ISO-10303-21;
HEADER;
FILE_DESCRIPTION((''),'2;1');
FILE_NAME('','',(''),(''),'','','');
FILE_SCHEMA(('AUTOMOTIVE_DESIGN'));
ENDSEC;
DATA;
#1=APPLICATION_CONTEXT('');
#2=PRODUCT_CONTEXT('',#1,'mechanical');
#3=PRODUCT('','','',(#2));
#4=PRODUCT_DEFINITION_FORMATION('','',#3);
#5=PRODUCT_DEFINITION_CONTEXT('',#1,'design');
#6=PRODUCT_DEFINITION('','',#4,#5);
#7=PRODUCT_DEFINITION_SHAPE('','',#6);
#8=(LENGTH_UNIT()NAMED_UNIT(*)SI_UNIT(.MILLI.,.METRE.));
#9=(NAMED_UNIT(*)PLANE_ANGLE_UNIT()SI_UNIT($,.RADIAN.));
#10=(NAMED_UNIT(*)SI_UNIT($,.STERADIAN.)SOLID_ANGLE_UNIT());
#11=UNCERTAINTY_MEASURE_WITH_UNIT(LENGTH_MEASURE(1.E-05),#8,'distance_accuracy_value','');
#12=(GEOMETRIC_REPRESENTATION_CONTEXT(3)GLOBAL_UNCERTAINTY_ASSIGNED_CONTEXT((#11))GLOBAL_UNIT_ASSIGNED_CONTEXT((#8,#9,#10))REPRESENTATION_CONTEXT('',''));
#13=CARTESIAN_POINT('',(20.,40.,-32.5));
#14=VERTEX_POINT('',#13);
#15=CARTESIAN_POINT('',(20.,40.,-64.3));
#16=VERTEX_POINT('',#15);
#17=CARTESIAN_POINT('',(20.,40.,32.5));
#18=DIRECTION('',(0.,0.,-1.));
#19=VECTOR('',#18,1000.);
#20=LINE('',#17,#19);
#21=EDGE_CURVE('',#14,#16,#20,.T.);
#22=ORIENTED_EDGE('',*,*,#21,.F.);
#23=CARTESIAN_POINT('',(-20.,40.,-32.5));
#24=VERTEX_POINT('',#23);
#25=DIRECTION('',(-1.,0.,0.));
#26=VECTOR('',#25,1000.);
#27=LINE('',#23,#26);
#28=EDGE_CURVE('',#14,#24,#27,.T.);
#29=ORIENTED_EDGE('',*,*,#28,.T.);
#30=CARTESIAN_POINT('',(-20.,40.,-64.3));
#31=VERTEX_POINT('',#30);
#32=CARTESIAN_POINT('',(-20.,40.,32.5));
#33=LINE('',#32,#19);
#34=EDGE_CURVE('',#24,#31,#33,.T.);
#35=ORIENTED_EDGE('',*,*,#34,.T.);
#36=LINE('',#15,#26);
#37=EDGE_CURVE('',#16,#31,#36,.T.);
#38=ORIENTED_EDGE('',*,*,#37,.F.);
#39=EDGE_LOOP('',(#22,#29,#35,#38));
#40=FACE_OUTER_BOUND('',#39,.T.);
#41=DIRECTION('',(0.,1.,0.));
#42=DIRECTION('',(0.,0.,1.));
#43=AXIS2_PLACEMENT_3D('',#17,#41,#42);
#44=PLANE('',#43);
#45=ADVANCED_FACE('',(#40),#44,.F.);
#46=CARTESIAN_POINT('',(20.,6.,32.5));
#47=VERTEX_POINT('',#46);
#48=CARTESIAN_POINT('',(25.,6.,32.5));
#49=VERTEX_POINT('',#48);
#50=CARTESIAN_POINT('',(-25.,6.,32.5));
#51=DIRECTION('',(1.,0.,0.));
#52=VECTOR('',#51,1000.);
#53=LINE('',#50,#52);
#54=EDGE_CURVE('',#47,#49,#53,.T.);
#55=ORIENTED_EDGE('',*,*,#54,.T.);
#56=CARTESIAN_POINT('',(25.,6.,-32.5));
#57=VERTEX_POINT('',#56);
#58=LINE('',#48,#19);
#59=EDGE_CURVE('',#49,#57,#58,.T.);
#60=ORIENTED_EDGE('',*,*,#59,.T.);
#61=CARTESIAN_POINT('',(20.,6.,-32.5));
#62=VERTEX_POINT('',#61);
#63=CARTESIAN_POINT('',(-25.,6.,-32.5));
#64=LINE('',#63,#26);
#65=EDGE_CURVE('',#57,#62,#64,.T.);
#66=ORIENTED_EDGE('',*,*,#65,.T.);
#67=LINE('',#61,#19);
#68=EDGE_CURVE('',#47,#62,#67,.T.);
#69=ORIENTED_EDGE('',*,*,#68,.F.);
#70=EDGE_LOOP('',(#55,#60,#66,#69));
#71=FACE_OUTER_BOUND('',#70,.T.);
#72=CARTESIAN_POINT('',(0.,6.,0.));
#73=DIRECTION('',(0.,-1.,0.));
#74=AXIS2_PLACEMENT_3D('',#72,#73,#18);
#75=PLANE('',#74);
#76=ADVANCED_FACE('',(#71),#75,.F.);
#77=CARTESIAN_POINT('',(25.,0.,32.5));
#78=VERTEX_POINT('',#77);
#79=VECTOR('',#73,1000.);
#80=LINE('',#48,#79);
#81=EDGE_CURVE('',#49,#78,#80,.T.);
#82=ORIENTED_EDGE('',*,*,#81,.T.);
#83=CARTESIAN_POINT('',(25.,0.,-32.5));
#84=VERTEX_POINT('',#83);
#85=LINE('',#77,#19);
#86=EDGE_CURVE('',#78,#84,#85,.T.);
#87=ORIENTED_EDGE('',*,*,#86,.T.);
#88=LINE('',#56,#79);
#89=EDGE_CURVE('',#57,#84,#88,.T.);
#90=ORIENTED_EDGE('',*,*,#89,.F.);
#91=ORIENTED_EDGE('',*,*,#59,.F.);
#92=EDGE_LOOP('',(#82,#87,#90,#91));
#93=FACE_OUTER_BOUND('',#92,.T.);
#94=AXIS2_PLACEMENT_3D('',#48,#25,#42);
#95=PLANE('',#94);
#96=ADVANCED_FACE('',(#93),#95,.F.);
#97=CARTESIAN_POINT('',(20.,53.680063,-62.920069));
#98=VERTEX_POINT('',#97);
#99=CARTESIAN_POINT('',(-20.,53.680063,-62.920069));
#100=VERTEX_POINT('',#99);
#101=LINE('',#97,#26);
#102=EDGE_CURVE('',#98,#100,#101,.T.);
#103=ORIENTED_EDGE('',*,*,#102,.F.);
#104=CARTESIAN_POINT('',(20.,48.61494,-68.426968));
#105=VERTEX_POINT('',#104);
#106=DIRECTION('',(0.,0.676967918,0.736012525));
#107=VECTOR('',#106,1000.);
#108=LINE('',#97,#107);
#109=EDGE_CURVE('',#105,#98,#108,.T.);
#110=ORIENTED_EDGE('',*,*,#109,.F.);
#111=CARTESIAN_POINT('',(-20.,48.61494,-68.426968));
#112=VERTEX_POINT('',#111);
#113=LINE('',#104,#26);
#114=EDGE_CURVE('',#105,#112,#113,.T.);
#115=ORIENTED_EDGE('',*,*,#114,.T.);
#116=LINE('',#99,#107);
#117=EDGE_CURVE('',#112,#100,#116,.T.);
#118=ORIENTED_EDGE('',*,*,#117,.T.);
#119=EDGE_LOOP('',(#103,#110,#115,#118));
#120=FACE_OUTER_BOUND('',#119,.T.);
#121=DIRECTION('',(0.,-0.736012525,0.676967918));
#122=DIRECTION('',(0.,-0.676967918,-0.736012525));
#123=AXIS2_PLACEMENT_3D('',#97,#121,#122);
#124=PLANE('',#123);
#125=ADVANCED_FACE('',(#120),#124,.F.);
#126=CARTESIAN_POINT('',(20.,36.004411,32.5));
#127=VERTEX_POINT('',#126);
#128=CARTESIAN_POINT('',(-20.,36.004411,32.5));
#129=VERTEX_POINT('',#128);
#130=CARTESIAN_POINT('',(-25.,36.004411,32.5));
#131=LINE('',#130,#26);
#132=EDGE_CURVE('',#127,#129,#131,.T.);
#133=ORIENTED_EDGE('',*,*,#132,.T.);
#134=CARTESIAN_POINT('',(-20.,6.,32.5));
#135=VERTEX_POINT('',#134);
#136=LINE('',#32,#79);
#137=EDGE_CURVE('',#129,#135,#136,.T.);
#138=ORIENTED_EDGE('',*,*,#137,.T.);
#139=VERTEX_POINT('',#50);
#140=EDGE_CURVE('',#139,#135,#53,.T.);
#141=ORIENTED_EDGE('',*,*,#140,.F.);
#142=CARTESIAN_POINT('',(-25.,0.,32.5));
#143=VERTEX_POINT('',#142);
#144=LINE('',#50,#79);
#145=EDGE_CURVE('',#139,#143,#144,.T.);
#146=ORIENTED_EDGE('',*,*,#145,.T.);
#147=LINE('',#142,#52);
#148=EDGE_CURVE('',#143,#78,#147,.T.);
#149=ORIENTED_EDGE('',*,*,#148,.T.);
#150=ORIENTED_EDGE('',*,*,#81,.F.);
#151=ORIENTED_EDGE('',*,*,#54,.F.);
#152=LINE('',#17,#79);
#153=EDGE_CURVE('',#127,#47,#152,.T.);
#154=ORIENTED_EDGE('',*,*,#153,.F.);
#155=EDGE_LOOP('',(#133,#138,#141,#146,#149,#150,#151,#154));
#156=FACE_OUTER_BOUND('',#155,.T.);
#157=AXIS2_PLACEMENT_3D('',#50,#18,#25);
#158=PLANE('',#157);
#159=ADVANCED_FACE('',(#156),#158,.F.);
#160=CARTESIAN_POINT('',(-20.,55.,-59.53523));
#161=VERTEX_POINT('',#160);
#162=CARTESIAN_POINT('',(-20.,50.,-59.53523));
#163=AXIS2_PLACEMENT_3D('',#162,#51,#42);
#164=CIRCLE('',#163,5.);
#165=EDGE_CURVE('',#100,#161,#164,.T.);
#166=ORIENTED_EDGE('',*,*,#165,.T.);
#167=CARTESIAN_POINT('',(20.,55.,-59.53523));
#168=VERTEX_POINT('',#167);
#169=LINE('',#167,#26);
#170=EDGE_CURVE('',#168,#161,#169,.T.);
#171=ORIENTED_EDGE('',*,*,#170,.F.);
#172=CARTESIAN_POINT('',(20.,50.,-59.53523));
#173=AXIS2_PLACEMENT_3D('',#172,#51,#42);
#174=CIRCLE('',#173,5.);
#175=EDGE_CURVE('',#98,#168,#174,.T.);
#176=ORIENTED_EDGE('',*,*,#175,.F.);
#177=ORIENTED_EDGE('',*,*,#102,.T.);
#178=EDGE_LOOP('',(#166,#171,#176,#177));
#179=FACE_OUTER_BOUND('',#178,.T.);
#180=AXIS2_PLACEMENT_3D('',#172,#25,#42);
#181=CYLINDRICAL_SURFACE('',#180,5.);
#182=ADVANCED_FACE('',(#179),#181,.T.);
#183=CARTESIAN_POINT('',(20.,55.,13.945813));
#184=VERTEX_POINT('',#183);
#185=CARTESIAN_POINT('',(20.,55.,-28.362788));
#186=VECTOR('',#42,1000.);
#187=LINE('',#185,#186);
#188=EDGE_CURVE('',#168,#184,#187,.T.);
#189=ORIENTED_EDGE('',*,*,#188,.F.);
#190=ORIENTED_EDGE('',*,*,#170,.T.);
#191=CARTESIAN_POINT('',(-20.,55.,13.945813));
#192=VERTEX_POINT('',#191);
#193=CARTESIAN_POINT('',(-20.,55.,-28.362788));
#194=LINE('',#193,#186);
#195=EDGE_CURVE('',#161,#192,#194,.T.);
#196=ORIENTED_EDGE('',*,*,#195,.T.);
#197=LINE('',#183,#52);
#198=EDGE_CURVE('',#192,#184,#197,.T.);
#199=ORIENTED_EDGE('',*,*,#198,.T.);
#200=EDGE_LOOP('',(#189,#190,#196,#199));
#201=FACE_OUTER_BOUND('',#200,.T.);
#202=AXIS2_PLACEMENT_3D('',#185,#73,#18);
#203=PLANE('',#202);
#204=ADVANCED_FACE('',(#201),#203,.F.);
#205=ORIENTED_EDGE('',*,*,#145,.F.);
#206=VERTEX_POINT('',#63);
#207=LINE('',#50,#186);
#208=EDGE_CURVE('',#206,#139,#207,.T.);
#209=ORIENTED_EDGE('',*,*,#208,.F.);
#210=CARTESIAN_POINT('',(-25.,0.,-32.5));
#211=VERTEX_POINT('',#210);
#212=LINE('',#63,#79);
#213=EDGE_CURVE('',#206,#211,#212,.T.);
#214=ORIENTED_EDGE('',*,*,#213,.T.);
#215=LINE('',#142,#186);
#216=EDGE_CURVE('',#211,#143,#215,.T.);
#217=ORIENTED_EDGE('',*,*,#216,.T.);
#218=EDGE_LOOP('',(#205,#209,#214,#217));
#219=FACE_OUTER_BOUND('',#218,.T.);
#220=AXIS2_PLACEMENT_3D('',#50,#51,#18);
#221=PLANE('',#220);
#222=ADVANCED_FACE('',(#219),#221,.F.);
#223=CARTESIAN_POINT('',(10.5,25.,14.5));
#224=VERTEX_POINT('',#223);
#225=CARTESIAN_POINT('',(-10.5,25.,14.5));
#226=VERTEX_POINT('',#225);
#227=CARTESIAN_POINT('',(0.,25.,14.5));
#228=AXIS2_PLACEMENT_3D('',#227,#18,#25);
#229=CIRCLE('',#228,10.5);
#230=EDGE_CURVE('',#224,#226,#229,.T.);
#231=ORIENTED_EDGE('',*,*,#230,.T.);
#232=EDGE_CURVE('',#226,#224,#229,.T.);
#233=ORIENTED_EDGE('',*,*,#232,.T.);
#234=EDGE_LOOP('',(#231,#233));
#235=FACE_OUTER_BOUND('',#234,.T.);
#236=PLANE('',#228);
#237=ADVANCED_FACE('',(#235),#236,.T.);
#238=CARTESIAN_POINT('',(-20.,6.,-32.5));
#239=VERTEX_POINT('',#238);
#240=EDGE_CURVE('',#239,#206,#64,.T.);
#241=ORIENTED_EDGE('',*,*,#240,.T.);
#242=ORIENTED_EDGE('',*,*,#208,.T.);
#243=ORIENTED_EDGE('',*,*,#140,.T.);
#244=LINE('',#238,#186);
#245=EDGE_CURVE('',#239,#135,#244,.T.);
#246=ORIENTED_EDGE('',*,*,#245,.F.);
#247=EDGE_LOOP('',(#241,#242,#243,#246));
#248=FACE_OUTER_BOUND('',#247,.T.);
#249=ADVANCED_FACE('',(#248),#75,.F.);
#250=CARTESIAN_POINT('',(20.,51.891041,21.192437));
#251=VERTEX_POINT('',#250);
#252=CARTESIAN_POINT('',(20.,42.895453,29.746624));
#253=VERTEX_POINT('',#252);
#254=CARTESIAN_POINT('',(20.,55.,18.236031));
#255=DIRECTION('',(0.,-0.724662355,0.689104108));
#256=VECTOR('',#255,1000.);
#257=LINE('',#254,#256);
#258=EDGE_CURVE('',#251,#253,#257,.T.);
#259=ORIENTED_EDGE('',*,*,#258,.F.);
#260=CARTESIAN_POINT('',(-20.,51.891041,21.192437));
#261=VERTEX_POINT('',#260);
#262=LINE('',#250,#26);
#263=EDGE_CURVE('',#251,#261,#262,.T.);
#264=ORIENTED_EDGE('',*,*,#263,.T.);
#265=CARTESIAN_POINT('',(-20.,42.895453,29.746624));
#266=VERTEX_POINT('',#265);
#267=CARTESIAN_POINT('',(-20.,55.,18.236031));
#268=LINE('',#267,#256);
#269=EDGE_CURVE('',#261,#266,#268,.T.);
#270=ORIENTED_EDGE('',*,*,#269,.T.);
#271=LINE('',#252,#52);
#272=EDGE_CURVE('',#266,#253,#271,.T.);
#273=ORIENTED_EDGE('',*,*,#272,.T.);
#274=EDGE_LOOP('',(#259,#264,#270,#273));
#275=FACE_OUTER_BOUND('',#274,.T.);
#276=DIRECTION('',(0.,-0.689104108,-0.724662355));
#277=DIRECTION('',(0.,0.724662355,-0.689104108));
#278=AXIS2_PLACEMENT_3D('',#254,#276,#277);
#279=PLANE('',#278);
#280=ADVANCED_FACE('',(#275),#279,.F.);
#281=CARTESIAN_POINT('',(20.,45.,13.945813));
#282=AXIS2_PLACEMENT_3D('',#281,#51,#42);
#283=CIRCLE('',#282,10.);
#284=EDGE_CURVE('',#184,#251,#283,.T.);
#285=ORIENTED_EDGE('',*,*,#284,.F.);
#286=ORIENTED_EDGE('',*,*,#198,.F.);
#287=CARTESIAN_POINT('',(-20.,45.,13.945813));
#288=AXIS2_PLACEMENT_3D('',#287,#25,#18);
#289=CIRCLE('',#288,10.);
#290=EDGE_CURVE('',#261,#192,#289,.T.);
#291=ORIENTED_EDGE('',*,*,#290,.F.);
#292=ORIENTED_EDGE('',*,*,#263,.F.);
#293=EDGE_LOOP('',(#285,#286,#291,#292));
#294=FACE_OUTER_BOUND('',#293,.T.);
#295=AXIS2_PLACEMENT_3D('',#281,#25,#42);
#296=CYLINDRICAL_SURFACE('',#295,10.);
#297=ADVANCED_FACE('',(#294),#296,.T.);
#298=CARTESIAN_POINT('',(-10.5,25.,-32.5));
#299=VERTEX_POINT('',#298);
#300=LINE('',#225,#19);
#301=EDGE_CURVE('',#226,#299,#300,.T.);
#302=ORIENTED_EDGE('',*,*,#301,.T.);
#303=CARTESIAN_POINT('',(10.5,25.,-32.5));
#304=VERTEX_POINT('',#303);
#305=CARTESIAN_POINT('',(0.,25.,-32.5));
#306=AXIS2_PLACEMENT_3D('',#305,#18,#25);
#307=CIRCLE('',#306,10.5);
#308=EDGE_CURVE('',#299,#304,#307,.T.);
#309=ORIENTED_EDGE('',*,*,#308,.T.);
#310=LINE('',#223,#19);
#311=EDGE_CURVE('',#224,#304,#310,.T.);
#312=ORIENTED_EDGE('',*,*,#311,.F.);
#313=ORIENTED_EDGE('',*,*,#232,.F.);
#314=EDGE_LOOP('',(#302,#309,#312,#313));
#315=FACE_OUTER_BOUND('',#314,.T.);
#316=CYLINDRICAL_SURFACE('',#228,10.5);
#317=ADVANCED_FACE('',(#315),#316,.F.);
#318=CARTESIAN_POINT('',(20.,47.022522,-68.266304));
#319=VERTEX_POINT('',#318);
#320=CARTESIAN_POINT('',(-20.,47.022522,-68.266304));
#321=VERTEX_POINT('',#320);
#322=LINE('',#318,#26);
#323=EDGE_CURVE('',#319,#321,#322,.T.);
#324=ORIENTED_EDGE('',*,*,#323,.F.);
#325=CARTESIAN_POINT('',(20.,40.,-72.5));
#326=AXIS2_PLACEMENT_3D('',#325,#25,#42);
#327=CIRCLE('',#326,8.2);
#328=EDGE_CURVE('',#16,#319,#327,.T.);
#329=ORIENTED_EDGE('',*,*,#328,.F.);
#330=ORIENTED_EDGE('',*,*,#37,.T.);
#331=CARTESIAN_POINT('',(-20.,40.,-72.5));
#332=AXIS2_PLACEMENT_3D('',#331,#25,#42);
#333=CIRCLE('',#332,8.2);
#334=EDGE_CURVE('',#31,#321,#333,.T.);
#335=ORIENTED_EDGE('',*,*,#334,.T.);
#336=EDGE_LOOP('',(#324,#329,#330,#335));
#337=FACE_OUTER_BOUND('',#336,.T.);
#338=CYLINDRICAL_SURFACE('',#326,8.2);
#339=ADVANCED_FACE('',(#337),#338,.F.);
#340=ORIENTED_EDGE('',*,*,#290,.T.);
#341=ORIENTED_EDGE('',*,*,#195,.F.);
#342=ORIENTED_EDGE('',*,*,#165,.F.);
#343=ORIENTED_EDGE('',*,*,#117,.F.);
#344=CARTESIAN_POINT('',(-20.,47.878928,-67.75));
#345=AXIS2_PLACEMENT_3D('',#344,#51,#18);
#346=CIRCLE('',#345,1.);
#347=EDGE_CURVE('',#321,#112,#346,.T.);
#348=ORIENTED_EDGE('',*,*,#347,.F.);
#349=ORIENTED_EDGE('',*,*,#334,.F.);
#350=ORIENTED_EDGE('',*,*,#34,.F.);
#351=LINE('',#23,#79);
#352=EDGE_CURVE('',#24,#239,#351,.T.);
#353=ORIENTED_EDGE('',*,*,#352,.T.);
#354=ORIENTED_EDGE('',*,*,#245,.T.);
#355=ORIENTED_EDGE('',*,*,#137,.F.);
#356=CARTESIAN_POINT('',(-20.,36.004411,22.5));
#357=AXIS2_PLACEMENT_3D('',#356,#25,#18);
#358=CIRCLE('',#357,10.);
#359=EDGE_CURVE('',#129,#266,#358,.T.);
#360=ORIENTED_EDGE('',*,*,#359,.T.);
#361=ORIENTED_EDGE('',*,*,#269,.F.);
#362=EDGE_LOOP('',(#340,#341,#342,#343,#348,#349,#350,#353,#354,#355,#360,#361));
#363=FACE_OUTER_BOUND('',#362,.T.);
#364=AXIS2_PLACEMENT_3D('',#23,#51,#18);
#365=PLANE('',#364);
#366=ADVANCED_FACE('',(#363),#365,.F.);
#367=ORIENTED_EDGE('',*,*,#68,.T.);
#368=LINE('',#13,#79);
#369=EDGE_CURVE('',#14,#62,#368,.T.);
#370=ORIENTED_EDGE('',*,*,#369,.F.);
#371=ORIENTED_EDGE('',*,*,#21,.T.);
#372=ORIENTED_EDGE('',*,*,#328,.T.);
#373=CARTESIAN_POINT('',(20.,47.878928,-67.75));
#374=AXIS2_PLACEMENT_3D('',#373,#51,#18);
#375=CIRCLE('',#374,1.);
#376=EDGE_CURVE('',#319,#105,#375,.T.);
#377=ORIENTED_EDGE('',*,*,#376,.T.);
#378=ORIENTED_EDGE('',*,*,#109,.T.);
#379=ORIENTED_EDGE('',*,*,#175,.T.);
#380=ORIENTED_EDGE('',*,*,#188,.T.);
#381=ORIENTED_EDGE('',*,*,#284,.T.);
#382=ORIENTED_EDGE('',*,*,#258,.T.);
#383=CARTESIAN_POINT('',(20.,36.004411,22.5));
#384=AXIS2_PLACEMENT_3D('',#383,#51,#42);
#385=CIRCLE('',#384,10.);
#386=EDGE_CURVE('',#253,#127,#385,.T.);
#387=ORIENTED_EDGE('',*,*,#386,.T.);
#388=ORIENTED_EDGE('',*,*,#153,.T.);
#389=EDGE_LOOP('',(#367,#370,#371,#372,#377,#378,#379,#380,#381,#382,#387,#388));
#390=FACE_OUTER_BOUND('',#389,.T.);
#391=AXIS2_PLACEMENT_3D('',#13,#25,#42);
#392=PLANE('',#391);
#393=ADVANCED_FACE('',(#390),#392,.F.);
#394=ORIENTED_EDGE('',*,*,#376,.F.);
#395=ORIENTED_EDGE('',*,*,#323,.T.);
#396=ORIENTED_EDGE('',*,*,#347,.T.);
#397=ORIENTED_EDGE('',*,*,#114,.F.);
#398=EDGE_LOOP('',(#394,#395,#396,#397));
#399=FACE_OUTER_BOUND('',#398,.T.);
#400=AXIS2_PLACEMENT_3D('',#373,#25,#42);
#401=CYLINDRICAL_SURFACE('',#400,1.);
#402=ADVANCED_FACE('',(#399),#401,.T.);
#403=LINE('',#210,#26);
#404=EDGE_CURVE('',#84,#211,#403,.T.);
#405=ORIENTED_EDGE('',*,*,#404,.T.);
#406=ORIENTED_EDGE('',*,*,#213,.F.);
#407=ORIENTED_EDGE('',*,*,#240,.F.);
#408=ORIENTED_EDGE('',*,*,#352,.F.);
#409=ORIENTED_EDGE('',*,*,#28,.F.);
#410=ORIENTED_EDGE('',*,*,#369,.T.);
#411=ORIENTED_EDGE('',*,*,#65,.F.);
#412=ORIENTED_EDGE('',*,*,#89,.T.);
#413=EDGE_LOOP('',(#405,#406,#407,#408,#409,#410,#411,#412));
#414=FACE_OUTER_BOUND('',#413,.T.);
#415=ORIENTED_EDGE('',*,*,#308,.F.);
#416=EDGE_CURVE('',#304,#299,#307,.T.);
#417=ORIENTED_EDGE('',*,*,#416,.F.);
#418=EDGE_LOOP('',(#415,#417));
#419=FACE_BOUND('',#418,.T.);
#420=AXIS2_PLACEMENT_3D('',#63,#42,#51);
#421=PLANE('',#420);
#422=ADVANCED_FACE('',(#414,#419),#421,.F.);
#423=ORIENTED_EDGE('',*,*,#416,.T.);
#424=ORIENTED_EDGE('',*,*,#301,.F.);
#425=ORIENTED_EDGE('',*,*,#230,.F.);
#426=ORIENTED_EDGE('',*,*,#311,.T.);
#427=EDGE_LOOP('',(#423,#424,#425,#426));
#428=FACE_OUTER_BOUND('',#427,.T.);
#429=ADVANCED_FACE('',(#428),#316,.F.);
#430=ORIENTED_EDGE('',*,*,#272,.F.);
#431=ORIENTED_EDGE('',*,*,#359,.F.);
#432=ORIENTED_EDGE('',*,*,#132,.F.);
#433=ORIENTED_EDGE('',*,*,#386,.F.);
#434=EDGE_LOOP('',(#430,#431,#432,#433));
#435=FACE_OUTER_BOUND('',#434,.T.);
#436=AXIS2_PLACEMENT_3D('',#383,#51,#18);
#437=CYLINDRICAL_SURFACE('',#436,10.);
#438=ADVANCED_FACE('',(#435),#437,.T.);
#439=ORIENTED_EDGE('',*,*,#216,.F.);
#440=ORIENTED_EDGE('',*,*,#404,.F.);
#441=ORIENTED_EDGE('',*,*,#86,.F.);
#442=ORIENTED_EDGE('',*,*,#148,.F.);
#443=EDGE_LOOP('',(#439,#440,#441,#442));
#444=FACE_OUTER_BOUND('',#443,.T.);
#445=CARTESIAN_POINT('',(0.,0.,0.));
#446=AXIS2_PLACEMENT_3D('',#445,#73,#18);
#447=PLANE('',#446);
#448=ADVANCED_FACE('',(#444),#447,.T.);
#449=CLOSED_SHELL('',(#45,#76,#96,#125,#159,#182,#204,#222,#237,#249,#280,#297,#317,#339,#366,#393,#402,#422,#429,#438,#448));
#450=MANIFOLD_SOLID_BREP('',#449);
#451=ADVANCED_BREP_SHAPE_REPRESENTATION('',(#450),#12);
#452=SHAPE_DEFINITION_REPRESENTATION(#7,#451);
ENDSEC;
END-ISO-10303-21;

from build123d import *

# Parameters (mm, degrees)
SKETCH1_W           = 50
SKETCH1_H           = 65
BOSS_EXTRUDE1_DEPTH = 6
SKETCH2_W           = 40
SKETCH2_H           = 65
BOSS_EXTRUDE2_DEPTH = 34
SKETCH3_R           = 10.5
CUT_EXTRUDE1_DEPTH  = 47
BOSS_EXTRUDE3_DEPTH = 20
FILLET1_R           = 10


with BuildPart() as part:
    # Sketch1 → Boss-Extrude1 (new body)
    with BuildSketch(Plane(origin=(0, 0, 0), x_dir=(1, 0, 0), z_dir=(0, 1, 0))):
        Rectangle(SKETCH1_W, SKETCH1_H)
    extrude(amount=BOSS_EXTRUDE1_DEPTH)

    # Sketch2 → Boss-Extrude2 (add)
    with BuildSketch(Plane(origin=(0, 6, 0), x_dir=(1, 0, 0), z_dir=(0, 1, 0))):
        Rectangle(SKETCH2_W, SKETCH2_H)
    extrude(amount=BOSS_EXTRUDE2_DEPTH)

    # Sketch3 → Cut-Extrude1 (cut)
    with BuildSketch(Plane(origin=(0, 0, -32.5), x_dir=(-1, 0, 0), z_dir=(0, 0, -1))):
        with Locations((0, 25)):
            Circle(SKETCH3_R)
    extrude(amount=-CUT_EXTRUDE1_DEPTH, mode=Mode.SUBTRACT)

    # Sketch4 → Boss-Extrude3 (add, symmetric)
    with BuildSketch(Plane(origin=(0, 0, 0), x_dir=(0, 0, -1), z_dir=(1, 0, 0))):
        with BuildLine():
            Line((-32.5, 40), (64.3, 40))
            ThreePointArc((64.3, 40), (65.360101389, 44.032598148), (68.266304348, 47.022522419))
            ThreePointArc((68.266304348, 47.022522419), (68.744948846, 47.778544361), (68.426967918, 48.614940117))
            Line((68.426967918, 48.614940117), (62.920069424, 53.680062627))
            ThreePointArc((62.920069424, 53.680062627), (61.351776951, 54.658342685), (59.535229833, 55))
            Line((59.535229833, 55), (28.36278807, 55))
            Line((28.36278807, 55), (-18.236030661, 55))
            Line((-18.236030661, 55), (-32.5, 40))
        make_face()
    extrude(amount=BOSS_EXTRUDE3_DEPTH, both=True)

    # Fillet1
    fillet1_edges = [part.edges().sort_by_distance(p)[0] for p in [
        (0, 40, 32.5),
        (0, 55, 18.236030661),
    ]]
    fillet(fillet1_edges, radius=FILLET1_R)


solid = part.part
